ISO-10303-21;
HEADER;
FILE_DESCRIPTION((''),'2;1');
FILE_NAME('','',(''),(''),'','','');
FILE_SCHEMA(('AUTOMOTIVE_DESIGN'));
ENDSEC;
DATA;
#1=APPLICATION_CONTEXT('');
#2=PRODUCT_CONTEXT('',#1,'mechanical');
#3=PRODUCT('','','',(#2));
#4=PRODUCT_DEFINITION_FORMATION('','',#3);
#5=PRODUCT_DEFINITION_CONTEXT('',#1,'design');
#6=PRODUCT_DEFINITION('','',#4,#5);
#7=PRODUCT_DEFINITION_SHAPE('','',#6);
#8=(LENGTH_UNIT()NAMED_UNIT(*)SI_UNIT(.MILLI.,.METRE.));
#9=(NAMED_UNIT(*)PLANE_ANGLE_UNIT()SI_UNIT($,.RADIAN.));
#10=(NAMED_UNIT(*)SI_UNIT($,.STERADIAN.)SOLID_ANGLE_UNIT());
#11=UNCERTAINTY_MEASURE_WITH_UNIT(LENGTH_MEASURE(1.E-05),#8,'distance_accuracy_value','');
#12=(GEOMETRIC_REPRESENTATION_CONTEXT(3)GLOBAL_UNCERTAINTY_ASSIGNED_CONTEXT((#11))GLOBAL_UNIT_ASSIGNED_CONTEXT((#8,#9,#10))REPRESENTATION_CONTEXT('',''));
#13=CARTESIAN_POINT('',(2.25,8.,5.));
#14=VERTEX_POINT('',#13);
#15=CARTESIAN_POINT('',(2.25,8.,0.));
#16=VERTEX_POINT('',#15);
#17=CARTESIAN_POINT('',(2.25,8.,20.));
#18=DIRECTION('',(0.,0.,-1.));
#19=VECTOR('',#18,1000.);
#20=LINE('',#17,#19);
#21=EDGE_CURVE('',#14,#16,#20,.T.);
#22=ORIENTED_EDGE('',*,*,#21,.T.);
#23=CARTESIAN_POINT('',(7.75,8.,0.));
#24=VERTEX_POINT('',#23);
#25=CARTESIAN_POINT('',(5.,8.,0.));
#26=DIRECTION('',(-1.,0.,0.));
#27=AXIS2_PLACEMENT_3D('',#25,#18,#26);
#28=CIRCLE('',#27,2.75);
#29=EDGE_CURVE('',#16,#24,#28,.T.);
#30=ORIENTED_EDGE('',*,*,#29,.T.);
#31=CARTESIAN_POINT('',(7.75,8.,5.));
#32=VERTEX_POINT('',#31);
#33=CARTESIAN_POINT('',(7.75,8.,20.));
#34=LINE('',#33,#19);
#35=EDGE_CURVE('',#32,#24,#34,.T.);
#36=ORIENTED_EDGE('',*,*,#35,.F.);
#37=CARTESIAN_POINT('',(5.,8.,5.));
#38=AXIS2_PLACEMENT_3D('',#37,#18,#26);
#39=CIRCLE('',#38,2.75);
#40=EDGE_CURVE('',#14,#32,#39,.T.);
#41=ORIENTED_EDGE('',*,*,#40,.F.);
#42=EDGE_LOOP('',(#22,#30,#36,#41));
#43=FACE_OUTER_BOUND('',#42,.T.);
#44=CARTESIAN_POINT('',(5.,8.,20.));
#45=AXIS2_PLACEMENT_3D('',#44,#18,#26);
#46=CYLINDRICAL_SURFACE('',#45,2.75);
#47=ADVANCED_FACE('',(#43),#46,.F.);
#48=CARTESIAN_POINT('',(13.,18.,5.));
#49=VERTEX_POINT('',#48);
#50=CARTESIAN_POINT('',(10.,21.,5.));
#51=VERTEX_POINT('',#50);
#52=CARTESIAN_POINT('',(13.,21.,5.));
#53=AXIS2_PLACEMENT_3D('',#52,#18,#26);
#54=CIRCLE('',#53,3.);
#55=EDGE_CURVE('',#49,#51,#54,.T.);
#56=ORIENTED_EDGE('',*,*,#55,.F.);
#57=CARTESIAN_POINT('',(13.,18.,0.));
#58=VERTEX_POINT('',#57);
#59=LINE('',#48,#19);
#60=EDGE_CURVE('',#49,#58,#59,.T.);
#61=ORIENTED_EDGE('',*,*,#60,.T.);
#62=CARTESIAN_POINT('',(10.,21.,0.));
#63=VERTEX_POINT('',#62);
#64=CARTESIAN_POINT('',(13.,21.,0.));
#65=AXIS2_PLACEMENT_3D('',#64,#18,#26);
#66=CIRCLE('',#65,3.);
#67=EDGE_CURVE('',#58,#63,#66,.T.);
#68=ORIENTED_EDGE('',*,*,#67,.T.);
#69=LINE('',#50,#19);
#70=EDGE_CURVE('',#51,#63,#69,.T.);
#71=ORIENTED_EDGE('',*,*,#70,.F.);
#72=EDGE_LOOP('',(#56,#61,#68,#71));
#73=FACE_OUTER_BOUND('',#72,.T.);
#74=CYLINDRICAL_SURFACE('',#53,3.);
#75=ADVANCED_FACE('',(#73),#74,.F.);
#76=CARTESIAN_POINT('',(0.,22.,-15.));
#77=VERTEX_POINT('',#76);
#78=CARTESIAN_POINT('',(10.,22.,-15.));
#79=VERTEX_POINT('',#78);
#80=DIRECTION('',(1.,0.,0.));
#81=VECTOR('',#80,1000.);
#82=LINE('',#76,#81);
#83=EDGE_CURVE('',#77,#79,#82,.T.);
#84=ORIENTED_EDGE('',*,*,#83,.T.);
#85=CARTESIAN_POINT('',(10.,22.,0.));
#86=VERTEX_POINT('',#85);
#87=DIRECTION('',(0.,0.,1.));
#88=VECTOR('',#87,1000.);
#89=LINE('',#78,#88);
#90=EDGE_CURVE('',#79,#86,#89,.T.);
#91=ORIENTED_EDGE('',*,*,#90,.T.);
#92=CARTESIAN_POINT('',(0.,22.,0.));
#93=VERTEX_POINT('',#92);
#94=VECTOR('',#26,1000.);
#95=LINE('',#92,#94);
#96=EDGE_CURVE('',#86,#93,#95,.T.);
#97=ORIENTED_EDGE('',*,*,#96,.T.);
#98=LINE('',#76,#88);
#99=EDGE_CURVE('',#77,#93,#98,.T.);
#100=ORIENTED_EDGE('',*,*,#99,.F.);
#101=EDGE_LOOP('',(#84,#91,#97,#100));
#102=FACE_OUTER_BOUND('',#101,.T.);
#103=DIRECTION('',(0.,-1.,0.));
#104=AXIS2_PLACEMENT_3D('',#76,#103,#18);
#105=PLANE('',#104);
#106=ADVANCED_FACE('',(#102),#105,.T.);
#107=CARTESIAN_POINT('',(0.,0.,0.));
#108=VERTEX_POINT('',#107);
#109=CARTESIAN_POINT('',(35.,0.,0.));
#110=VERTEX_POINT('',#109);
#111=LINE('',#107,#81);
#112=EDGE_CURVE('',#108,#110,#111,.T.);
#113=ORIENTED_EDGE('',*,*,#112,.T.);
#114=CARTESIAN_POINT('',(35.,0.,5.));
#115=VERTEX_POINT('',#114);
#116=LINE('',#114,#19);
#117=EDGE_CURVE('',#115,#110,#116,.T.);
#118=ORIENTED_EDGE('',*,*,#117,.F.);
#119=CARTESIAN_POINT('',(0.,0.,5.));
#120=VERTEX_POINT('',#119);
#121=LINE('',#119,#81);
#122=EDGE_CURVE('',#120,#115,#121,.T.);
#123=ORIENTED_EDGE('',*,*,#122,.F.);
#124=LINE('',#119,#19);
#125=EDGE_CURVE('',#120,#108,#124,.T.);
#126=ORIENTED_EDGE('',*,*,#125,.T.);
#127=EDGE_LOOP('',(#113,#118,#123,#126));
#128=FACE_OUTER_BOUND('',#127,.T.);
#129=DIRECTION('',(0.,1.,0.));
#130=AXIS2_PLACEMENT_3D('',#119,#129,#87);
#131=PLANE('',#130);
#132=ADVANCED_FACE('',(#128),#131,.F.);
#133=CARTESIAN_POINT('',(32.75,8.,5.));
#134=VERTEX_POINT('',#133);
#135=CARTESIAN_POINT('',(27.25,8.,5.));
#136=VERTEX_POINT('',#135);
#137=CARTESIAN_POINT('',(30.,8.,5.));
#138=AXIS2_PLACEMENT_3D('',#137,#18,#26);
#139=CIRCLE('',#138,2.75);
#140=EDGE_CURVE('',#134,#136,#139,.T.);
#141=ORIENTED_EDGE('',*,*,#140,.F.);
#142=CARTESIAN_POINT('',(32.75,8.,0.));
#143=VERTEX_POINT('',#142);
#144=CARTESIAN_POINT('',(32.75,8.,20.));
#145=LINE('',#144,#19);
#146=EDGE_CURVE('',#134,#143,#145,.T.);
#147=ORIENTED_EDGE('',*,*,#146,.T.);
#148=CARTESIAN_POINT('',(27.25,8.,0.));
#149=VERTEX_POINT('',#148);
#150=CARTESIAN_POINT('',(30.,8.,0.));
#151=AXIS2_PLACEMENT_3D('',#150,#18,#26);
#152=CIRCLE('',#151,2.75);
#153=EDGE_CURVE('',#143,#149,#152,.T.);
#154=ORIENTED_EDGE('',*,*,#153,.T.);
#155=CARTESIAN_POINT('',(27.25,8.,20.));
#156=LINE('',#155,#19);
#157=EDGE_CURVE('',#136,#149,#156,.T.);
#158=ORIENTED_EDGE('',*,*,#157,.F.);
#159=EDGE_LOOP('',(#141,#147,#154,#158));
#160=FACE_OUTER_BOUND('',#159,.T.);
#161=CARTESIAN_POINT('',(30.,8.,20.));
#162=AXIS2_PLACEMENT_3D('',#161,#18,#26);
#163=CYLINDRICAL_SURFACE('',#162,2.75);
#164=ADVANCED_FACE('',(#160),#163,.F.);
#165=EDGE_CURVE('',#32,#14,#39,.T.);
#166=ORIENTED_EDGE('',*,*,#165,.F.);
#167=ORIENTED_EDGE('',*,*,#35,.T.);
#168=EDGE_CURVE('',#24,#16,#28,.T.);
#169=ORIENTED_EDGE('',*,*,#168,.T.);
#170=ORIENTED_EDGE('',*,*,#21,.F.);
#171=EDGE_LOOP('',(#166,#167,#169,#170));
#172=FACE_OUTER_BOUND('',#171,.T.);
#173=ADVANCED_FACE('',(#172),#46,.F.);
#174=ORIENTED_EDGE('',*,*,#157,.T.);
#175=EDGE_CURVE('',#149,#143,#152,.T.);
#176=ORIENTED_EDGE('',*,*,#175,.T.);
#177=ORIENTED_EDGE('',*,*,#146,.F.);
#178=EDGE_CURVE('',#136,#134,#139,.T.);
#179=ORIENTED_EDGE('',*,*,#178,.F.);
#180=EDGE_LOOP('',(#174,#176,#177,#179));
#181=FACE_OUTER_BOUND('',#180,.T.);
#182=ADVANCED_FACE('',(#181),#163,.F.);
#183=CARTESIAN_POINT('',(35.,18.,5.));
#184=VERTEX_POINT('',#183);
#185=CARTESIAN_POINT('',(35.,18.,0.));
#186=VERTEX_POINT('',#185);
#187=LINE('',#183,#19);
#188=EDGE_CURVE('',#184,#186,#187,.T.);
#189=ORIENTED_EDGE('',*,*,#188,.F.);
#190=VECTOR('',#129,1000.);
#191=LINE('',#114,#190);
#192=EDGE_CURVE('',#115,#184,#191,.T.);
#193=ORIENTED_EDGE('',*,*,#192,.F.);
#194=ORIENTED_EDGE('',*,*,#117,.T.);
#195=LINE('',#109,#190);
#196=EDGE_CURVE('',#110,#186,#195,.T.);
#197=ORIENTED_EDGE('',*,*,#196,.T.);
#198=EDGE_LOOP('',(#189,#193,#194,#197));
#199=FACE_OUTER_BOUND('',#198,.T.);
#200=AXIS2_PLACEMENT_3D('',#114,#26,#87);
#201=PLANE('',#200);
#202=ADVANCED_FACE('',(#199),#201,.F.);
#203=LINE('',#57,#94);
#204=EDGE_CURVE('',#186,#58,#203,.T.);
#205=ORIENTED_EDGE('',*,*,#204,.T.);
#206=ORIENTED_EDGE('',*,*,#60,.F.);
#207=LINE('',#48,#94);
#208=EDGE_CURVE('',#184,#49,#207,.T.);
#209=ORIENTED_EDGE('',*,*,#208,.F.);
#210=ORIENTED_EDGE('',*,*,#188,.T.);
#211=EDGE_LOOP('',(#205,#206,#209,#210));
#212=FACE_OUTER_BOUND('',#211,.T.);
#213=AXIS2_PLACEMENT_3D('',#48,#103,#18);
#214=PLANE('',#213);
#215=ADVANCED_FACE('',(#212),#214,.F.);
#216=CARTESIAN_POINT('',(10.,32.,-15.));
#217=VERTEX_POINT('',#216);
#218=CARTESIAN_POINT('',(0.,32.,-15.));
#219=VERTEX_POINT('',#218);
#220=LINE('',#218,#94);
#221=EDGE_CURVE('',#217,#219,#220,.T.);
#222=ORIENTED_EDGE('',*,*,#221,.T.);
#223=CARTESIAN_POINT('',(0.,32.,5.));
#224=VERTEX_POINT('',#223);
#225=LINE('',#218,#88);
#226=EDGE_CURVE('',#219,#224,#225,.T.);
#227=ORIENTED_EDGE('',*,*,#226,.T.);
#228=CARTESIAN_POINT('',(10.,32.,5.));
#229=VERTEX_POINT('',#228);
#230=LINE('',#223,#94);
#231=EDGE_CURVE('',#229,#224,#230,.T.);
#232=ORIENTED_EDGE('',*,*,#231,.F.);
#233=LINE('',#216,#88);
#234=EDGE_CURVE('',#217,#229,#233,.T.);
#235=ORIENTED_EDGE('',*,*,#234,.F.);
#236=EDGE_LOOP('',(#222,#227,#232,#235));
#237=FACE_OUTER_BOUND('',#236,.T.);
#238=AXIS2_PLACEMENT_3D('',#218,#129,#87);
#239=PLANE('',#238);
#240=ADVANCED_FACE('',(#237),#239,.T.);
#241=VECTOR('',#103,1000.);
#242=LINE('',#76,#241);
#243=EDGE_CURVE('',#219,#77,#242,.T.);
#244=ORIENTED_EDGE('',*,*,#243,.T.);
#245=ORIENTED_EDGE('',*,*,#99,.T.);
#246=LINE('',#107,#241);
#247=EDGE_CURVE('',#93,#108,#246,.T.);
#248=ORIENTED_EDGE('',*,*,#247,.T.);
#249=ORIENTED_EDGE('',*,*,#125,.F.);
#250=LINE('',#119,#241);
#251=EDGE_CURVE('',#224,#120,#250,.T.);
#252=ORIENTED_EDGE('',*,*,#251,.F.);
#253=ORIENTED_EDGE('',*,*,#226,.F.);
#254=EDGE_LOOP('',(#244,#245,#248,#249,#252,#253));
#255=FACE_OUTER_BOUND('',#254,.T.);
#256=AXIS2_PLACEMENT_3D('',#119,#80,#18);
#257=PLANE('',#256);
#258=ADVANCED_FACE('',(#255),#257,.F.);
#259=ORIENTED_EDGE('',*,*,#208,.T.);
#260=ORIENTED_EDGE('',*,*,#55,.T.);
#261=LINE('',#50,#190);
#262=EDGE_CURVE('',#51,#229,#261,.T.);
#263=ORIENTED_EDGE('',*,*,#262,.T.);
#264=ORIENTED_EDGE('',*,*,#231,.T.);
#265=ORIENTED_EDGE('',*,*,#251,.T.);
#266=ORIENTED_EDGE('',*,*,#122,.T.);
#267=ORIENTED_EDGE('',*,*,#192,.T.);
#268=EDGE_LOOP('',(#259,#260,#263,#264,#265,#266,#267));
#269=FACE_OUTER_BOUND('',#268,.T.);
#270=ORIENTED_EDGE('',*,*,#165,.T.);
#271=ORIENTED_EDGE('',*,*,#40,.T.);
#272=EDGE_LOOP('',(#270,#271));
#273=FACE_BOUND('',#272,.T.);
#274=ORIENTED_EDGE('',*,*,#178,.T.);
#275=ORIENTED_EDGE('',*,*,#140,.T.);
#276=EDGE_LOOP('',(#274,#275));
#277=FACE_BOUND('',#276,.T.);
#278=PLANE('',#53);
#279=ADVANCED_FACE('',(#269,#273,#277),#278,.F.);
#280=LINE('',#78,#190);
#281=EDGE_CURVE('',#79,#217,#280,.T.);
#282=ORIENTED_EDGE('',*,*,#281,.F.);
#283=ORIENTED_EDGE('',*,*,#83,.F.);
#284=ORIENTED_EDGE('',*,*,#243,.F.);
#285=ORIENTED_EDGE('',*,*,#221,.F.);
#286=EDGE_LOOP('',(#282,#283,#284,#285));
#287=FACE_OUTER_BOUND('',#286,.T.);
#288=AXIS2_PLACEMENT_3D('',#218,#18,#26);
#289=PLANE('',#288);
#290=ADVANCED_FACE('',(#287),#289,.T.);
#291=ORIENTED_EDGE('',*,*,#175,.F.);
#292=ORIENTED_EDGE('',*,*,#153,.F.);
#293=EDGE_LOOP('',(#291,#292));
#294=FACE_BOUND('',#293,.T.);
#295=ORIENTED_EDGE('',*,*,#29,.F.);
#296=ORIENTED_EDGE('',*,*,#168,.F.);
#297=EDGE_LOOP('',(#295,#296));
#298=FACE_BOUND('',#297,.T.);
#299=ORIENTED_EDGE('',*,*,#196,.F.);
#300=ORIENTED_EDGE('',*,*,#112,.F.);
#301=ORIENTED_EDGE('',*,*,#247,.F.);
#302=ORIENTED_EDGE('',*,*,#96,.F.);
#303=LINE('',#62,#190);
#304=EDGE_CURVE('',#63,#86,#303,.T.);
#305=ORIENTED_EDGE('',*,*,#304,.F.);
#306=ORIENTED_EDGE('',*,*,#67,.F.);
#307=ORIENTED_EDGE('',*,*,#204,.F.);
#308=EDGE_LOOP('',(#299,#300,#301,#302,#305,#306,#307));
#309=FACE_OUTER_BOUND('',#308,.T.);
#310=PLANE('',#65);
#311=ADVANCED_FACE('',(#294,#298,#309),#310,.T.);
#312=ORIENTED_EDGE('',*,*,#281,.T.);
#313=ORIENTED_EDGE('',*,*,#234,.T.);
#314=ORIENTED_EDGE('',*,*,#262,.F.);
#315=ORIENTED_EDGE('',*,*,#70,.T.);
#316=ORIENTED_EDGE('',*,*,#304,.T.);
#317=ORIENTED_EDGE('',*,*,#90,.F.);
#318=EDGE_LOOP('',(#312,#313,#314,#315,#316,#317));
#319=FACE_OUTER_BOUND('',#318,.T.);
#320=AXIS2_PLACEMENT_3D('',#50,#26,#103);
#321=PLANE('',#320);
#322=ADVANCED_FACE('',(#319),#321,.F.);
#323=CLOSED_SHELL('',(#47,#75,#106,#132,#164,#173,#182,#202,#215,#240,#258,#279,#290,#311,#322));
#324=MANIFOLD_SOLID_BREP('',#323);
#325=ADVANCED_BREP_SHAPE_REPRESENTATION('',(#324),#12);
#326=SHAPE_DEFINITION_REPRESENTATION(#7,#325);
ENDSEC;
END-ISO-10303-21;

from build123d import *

# Parameters (mm, degrees)
EXTRUDE_1_DEPTH     = 5
SKETCH_3_W          = 10
SKETCH_3_H          = 10
EXTRUDE_2_DEPTH     = 20
SKETCH_4_R          = 2.75
CUT_EXTRUDE_1_DEPTH = 20


with BuildPart() as part:
    # 草图1 → 凸台-拉伸1 (new body)
    with BuildSketch(Plane.XY):
        with BuildLine():
            Line((0, 0), (35, 0))
            Line((35, 0), (35, 18))
            Line((35, 18), (13, 18))
            ThreePointArc((13, 18), (10.878679656, 18.878679656), (10, 21))
            Line((10, 21), (10, 22))
            Line((10, 22), (0, 22))
            Line((0, 22), (0, 0))
        make_face()
    extrude(amount=EXTRUDE_1_DEPTH)

    # 草图3 → 凸台-拉伸2 (add)
    with BuildSketch(Plane.XY.offset(5)):
        with Locations((5, 27)):
            Rectangle(SKETCH_3_W, SKETCH_3_H)
    extrude(amount=-EXTRUDE_2_DEPTH)

    # 草图4 → 切除-拉伸1 (cut)
    with BuildSketch(Plane(origin=(0, 0, 0), x_dir=(-1, 0, 0), z_dir=(0, 0, -1))):
        with Locations((-30, 8)):
            Circle(SKETCH_4_R)
        with Locations((-5, 8)):
            Circle(SKETCH_4_R)
    extrude(amount=-CUT_EXTRUDE_1_DEPTH, mode=Mode.SUBTRACT)


solid = part.part
